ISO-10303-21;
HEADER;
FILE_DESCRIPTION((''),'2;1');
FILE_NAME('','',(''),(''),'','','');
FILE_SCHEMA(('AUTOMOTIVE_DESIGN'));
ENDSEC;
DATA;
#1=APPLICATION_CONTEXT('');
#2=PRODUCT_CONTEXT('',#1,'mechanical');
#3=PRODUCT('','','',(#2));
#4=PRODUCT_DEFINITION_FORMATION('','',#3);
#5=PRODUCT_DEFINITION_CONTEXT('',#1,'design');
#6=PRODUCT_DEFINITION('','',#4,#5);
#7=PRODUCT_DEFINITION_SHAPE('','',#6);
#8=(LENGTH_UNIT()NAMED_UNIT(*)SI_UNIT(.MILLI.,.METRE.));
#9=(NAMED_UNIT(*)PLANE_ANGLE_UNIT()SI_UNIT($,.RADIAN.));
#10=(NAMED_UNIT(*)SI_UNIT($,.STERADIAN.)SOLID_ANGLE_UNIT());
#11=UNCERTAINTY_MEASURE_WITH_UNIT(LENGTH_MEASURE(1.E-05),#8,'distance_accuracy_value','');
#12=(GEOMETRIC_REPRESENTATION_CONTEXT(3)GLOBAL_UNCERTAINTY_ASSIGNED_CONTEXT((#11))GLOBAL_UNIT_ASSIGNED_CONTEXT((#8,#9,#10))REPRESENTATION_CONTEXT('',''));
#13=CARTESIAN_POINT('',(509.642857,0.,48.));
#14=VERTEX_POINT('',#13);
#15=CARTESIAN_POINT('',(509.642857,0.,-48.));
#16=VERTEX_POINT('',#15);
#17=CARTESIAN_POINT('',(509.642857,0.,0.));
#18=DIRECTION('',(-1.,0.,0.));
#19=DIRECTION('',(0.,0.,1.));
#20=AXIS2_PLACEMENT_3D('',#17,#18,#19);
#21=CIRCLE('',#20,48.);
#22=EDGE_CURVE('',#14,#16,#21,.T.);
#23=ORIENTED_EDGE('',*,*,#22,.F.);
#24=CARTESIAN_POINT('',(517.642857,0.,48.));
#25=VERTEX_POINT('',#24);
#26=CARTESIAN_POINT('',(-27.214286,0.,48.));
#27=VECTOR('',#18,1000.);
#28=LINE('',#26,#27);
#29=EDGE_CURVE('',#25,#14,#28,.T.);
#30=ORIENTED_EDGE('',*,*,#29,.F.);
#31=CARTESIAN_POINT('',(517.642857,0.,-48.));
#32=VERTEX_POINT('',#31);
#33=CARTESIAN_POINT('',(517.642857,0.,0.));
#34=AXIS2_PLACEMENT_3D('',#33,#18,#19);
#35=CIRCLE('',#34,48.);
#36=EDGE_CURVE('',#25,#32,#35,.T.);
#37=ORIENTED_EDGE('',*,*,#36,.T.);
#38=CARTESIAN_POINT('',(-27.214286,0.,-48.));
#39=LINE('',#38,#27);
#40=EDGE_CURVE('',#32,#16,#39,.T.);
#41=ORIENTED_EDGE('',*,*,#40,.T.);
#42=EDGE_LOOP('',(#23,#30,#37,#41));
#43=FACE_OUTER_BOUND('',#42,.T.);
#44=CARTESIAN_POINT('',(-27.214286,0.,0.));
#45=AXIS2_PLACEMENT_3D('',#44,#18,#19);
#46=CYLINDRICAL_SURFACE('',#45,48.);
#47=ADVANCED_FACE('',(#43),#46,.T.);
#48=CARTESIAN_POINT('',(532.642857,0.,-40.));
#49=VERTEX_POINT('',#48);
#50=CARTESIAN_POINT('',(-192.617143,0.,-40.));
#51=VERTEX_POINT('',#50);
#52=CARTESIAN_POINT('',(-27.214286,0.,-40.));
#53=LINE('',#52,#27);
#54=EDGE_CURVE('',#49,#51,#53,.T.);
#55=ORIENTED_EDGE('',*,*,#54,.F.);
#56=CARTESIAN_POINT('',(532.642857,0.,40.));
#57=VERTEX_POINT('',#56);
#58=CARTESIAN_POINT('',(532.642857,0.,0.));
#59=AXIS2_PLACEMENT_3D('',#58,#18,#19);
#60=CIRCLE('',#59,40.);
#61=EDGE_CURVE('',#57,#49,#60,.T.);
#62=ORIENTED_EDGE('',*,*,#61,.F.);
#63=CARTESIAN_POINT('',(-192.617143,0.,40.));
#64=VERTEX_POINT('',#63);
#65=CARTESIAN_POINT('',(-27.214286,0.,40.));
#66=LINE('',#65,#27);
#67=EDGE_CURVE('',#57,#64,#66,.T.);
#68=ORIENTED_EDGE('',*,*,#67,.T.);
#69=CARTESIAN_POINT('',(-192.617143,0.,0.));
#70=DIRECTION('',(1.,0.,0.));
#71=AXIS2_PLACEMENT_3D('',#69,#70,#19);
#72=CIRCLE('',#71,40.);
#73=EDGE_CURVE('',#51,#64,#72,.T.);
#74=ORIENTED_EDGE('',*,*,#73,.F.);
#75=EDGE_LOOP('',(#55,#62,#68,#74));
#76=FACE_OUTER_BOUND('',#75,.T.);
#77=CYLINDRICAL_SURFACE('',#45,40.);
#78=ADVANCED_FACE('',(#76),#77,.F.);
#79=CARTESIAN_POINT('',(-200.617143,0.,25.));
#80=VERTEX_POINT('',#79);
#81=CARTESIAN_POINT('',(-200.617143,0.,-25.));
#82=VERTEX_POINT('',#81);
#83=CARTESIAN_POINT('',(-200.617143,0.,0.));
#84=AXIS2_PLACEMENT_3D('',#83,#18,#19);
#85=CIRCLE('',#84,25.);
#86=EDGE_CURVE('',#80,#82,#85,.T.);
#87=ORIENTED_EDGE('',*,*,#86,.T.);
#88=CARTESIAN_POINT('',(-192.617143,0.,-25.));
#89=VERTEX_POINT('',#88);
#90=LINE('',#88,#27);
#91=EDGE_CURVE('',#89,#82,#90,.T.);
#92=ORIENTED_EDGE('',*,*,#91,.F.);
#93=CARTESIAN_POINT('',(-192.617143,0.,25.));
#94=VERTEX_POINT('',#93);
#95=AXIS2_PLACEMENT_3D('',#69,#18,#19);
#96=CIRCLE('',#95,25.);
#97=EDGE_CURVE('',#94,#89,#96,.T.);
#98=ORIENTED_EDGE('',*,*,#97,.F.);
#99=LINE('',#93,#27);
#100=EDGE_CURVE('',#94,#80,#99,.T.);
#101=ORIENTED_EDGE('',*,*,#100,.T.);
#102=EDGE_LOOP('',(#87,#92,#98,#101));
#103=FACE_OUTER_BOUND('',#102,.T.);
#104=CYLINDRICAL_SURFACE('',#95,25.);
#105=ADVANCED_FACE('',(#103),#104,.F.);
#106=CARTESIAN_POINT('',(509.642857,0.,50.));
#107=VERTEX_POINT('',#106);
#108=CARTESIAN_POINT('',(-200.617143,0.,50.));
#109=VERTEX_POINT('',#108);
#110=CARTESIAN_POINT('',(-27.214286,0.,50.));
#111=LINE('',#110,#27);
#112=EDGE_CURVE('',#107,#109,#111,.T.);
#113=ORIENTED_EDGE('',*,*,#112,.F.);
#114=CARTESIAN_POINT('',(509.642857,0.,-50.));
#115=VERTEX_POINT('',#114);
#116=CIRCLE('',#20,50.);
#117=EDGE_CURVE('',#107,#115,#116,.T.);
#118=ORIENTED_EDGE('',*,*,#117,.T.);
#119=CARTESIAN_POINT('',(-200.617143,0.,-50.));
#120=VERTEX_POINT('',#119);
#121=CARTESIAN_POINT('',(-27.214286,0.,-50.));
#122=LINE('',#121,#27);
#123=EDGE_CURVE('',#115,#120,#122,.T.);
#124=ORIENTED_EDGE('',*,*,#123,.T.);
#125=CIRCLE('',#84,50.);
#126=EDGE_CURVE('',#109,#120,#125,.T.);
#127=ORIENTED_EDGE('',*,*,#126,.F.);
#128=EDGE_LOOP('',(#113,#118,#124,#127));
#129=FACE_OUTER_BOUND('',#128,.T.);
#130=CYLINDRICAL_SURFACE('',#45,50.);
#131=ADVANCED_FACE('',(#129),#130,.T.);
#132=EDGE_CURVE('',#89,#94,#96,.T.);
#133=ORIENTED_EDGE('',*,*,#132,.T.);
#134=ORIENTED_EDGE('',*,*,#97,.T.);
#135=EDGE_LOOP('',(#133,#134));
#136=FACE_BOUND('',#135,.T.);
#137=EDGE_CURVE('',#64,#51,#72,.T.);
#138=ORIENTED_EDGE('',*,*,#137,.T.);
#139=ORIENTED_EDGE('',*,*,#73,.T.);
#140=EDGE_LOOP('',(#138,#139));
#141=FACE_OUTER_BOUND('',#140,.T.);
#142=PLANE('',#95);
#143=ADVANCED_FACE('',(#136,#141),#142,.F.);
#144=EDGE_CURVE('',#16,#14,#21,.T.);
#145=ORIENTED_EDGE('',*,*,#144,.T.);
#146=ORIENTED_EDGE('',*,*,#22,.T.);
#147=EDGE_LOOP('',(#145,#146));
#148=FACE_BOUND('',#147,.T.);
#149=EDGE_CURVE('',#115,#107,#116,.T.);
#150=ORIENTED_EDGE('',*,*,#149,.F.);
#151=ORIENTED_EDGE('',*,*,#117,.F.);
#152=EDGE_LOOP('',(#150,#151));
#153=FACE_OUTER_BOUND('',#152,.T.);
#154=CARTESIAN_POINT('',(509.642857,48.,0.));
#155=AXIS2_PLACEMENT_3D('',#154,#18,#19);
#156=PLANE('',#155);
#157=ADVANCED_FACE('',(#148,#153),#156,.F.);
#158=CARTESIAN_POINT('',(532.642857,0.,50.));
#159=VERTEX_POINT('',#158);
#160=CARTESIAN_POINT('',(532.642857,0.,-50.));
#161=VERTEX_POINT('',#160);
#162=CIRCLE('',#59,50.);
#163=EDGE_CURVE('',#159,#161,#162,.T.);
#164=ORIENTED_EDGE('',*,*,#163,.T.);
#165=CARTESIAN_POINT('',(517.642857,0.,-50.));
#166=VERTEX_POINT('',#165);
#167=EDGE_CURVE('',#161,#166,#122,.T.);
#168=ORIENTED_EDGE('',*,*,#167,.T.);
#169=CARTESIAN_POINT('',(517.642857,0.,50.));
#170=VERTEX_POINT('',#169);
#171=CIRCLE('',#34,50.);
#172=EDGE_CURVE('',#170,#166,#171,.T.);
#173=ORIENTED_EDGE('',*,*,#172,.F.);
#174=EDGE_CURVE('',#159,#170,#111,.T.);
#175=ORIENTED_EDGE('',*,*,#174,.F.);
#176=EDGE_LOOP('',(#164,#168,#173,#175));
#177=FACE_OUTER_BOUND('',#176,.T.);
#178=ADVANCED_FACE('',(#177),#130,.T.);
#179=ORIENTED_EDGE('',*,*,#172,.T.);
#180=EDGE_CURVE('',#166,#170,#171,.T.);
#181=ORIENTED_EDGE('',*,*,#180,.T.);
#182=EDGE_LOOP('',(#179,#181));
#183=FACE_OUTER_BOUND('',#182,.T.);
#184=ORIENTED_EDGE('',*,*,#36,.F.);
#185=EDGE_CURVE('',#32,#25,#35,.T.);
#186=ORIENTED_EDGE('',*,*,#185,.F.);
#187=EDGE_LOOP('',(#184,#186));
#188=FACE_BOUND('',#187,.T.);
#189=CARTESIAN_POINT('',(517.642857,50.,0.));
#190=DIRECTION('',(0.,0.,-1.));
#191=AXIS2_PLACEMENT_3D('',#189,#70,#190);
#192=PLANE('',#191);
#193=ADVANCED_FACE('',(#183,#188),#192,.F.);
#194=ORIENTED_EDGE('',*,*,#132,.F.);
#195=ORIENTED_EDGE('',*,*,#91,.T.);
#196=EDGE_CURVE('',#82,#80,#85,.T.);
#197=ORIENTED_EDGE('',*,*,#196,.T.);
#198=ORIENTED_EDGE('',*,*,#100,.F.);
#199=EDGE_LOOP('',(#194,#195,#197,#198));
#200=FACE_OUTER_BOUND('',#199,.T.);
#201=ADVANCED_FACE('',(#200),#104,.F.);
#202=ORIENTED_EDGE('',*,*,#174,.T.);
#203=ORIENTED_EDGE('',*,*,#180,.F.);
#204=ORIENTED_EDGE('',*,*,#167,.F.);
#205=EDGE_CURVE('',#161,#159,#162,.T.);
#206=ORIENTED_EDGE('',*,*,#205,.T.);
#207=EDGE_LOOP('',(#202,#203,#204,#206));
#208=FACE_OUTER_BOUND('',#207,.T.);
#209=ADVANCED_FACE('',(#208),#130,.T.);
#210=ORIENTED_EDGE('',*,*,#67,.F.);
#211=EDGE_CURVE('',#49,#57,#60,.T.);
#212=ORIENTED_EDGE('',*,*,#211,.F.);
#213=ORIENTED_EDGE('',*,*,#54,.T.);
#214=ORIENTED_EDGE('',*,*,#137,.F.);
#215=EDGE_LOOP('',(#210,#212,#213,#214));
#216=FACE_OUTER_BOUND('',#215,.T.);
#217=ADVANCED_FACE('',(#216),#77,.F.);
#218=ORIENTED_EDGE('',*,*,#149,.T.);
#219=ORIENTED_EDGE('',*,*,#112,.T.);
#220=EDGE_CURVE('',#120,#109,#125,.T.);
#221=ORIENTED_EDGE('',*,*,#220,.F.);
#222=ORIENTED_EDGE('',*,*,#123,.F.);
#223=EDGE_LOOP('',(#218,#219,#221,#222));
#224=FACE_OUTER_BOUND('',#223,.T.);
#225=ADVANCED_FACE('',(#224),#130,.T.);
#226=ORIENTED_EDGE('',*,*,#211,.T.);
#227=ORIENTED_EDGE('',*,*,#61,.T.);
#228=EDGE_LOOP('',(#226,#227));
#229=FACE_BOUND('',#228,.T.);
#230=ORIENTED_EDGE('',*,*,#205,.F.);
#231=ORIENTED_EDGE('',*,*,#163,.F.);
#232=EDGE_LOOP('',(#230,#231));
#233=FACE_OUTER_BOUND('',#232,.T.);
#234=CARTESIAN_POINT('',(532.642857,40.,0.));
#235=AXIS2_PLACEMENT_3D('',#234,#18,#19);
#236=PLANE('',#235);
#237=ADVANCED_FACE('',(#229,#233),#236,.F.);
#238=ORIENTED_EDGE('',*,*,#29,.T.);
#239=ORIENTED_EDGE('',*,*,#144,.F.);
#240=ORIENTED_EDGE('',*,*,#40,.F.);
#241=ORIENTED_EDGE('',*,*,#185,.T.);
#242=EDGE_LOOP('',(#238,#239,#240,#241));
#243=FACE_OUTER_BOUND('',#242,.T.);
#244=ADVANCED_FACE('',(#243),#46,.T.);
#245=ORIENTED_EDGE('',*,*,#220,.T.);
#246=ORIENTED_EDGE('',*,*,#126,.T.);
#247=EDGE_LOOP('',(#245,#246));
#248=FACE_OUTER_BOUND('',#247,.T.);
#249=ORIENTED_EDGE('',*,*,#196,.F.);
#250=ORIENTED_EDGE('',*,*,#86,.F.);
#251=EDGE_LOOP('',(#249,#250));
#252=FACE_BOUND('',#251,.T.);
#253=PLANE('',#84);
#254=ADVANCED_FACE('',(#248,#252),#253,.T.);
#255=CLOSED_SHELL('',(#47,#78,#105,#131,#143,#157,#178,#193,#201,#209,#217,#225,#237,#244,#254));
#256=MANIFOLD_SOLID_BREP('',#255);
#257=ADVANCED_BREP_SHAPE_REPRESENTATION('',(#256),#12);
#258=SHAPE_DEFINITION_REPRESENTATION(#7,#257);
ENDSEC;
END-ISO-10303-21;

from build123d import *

# Parameters (mm, degrees)
EXTRUDE_START   = 200
SKETCH_3_R      = 50
SKETCH_3_R_2    = 40
EXTRUDE_1_DEPTH = 200
EXTRUDE_START_2 = -8
SKETCH_4_R      = 40
SKETCH_4_R_2    = 25
EXTRUDE_2_DEPTH = 8


with BuildPart() as part:
    # 草图2 → 旋转1 (revolve)
    with BuildSketch(Plane.XY, mode=Mode.PRIVATE) as revolve_1_sk:
        Polygon((-22.357142857, 40), (532.642857143, 40), (532.642857143, 50), (517.642857143, 50), (517.642857143, 48), (509.642857143, 48), (509.642857143, 50), (-0.617142857, 50), (-0.617142857, 48), (-8.617142857, 48), (-8.617142857, 50), (-22.357142857, 50), align=None)
    revolve(revolve_1_sk.sketch.rotate(Axis((-27.214285714, 0, 0), (1, 0, 0)), 90), axis=Axis((-27.214285714, 0, 0), (1, 0, 0)))

    # 草图3 → 凸台-拉伸1 (add)
    with BuildSketch(Plane.ZY.offset(0.617142857).offset(EXTRUDE_START)):
        Circle(SKETCH_3_R)
        Circle(SKETCH_3_R_2, mode=Mode.SUBTRACT)
    extrude(amount=-EXTRUDE_1_DEPTH)

    # 草图4 → 凸台-拉伸2 (add)
    with BuildSketch(Plane.ZY.offset(200.617142857).offset(EXTRUDE_START_2)):
        Circle(SKETCH_4_R)
        Circle(SKETCH_4_R_2, mode=Mode.SUBTRACT)
    extrude(amount=EXTRUDE_2_DEPTH)


solid = part.part
